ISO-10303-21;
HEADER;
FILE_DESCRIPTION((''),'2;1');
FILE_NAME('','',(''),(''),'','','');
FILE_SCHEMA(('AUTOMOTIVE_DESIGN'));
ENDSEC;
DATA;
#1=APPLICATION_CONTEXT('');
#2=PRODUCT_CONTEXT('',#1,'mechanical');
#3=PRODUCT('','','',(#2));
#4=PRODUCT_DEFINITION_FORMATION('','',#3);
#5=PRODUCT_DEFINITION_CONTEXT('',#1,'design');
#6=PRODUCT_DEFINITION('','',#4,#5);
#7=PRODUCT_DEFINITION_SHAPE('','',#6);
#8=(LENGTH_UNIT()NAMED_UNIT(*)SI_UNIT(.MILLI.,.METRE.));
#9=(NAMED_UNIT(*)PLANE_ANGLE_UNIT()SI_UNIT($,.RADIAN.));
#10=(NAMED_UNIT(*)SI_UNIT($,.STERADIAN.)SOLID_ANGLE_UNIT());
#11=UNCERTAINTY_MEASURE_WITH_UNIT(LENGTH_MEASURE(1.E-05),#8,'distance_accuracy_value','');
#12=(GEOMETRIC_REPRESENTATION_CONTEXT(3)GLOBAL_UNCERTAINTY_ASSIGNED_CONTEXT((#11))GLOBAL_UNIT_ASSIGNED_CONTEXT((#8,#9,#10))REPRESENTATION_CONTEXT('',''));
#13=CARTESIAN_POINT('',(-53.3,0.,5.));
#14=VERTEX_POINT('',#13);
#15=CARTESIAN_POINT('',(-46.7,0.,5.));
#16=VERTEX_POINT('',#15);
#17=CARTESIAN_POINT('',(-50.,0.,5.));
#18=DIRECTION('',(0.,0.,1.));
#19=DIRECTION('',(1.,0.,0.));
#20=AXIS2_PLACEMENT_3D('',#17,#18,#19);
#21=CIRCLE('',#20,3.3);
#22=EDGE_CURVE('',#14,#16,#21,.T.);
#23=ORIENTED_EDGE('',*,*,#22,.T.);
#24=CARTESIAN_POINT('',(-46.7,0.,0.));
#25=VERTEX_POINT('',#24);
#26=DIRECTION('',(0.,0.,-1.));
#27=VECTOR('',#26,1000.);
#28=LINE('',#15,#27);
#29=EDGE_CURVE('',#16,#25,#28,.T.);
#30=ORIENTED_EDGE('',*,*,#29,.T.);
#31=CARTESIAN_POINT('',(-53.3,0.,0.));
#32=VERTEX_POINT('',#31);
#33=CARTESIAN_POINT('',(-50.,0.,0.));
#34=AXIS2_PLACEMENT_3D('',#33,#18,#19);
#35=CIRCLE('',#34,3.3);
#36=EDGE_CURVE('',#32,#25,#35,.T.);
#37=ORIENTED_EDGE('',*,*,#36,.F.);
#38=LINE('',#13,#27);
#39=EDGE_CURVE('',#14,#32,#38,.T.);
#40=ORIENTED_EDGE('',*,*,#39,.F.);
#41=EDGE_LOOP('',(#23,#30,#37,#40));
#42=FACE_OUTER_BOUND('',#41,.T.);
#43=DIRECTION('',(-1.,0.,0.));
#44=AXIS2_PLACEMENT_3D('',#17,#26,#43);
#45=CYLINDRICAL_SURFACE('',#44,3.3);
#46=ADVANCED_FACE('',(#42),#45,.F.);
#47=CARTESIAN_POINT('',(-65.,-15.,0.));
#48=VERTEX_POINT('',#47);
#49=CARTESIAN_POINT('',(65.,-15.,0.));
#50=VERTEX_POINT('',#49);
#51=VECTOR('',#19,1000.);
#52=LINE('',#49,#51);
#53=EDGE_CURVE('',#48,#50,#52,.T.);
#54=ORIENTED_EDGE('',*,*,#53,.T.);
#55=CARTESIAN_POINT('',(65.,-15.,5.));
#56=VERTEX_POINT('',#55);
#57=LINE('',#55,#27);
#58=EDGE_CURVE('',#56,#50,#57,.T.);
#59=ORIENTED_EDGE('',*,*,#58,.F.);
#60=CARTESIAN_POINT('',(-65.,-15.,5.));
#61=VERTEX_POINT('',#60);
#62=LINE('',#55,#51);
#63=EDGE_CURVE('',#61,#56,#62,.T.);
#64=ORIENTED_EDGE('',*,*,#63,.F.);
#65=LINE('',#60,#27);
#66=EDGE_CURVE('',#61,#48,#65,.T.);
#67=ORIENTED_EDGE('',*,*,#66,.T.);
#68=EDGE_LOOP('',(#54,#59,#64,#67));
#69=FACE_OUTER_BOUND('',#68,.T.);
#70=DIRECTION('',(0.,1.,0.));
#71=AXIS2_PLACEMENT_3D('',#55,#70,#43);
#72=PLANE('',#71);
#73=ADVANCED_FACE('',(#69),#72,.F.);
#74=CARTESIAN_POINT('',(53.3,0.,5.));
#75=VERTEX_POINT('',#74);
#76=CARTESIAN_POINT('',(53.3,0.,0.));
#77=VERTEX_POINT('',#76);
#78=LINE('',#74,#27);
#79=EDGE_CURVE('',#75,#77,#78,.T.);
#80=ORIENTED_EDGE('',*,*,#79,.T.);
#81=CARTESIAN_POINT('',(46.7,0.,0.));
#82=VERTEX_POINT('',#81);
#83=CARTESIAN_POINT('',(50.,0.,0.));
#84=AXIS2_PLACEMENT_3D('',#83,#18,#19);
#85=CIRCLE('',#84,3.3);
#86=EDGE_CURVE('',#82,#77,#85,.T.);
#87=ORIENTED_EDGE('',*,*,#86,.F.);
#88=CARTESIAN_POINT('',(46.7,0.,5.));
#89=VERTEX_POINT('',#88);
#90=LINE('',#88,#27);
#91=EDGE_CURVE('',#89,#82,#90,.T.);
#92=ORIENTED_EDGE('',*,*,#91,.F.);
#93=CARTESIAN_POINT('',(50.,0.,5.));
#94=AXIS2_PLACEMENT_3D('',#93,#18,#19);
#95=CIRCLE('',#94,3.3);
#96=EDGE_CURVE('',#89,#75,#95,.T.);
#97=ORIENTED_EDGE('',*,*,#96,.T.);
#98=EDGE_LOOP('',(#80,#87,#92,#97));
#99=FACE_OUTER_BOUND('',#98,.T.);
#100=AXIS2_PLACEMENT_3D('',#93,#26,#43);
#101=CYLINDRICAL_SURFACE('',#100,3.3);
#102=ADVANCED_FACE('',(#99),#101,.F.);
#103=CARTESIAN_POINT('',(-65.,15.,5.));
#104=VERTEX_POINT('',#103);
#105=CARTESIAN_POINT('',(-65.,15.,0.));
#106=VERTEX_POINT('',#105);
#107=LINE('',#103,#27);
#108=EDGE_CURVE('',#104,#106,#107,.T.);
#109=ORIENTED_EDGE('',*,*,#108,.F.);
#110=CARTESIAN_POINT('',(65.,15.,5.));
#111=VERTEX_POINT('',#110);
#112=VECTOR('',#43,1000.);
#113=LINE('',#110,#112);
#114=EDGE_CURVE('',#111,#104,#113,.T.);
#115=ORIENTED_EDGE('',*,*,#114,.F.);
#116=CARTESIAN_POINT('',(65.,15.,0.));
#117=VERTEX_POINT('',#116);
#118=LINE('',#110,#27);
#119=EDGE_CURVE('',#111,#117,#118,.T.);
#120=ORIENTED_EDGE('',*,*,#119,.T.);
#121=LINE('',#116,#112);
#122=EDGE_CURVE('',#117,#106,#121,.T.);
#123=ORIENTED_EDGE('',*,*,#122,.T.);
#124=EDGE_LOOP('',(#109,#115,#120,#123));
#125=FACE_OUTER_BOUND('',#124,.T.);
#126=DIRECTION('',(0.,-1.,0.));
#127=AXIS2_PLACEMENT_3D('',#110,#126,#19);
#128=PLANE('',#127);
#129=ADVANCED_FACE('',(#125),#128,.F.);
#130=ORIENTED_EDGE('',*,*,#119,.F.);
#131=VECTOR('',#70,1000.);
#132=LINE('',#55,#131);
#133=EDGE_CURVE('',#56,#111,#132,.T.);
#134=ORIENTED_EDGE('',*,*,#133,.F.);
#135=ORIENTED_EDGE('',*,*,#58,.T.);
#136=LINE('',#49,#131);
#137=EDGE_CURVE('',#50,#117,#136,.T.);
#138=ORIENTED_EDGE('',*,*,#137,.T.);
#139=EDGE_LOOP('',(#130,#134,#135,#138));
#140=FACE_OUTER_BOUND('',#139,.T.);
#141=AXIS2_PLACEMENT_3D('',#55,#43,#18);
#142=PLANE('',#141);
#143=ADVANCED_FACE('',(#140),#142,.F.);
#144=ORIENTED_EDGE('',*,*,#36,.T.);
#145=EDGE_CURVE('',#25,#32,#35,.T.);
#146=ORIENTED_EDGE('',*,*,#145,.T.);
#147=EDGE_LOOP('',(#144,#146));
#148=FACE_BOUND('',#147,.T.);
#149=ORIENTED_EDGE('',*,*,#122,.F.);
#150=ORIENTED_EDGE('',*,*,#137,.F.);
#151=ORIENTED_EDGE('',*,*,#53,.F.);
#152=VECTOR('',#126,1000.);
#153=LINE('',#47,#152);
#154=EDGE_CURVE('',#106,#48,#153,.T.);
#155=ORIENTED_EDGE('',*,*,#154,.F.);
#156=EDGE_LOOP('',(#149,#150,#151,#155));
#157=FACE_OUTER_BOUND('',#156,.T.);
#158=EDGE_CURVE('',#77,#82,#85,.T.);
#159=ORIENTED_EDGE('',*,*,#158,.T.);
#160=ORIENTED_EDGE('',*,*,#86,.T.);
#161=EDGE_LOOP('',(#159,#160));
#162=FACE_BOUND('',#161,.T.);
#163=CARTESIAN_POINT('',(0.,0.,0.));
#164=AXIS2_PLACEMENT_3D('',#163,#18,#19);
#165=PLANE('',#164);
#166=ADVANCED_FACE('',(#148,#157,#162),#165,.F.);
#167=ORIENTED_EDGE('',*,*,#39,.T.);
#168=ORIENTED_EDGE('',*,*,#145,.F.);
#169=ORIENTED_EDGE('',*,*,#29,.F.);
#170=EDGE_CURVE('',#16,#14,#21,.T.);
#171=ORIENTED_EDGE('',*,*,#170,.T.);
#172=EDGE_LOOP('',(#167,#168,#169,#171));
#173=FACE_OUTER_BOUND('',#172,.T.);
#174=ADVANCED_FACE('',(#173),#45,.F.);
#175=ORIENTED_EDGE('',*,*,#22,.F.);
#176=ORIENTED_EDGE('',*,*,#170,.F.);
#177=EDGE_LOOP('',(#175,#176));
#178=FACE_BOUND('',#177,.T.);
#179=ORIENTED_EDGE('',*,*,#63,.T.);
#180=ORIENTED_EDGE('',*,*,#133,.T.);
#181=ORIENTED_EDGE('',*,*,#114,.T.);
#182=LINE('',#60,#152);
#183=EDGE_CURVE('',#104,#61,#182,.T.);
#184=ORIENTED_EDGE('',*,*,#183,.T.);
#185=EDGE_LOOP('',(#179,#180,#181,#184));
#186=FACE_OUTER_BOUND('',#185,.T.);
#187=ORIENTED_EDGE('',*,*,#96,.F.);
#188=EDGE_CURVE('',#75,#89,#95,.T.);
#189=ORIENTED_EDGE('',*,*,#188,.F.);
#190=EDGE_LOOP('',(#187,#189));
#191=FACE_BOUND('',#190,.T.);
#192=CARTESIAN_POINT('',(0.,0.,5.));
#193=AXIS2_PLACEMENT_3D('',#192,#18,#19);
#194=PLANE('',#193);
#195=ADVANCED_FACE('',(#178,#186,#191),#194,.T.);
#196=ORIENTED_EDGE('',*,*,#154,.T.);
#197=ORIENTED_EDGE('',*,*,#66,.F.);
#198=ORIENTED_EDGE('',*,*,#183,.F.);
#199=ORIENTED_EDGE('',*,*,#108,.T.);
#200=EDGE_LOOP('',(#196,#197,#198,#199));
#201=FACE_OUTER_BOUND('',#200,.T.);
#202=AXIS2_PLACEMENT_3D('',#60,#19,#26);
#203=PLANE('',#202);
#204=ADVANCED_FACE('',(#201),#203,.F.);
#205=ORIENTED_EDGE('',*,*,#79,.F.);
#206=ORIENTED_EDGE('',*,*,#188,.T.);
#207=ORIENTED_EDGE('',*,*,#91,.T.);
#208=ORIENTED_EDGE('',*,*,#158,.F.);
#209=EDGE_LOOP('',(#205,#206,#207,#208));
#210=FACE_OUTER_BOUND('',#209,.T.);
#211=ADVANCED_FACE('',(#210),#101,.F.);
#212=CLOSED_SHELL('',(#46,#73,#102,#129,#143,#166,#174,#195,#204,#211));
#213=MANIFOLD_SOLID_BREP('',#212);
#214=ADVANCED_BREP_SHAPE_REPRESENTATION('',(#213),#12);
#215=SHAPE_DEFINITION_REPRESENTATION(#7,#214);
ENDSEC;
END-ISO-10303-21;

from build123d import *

# Parameters (mm, degrees)
SKETCH_1_W      = 130
SKETCH_1_H      = 30
SKETCH_1_R      = 3.3
EXTRUDE_1_DEPTH = 5


with BuildPart() as part:
    # 草图1 → 凸台-拉伸1 (new body)
    with BuildSketch(Plane.XY):
        Rectangle(SKETCH_1_W, SKETCH_1_H)
        with Locations((-50, 0)):
            Circle(SKETCH_1_R, mode=Mode.SUBTRACT)
        with Locations((50, 0)):
            Circle(SKETCH_1_R, mode=Mode.SUBTRACT)
    extrude(amount=EXTRUDE_1_DEPTH)


solid = part.part
